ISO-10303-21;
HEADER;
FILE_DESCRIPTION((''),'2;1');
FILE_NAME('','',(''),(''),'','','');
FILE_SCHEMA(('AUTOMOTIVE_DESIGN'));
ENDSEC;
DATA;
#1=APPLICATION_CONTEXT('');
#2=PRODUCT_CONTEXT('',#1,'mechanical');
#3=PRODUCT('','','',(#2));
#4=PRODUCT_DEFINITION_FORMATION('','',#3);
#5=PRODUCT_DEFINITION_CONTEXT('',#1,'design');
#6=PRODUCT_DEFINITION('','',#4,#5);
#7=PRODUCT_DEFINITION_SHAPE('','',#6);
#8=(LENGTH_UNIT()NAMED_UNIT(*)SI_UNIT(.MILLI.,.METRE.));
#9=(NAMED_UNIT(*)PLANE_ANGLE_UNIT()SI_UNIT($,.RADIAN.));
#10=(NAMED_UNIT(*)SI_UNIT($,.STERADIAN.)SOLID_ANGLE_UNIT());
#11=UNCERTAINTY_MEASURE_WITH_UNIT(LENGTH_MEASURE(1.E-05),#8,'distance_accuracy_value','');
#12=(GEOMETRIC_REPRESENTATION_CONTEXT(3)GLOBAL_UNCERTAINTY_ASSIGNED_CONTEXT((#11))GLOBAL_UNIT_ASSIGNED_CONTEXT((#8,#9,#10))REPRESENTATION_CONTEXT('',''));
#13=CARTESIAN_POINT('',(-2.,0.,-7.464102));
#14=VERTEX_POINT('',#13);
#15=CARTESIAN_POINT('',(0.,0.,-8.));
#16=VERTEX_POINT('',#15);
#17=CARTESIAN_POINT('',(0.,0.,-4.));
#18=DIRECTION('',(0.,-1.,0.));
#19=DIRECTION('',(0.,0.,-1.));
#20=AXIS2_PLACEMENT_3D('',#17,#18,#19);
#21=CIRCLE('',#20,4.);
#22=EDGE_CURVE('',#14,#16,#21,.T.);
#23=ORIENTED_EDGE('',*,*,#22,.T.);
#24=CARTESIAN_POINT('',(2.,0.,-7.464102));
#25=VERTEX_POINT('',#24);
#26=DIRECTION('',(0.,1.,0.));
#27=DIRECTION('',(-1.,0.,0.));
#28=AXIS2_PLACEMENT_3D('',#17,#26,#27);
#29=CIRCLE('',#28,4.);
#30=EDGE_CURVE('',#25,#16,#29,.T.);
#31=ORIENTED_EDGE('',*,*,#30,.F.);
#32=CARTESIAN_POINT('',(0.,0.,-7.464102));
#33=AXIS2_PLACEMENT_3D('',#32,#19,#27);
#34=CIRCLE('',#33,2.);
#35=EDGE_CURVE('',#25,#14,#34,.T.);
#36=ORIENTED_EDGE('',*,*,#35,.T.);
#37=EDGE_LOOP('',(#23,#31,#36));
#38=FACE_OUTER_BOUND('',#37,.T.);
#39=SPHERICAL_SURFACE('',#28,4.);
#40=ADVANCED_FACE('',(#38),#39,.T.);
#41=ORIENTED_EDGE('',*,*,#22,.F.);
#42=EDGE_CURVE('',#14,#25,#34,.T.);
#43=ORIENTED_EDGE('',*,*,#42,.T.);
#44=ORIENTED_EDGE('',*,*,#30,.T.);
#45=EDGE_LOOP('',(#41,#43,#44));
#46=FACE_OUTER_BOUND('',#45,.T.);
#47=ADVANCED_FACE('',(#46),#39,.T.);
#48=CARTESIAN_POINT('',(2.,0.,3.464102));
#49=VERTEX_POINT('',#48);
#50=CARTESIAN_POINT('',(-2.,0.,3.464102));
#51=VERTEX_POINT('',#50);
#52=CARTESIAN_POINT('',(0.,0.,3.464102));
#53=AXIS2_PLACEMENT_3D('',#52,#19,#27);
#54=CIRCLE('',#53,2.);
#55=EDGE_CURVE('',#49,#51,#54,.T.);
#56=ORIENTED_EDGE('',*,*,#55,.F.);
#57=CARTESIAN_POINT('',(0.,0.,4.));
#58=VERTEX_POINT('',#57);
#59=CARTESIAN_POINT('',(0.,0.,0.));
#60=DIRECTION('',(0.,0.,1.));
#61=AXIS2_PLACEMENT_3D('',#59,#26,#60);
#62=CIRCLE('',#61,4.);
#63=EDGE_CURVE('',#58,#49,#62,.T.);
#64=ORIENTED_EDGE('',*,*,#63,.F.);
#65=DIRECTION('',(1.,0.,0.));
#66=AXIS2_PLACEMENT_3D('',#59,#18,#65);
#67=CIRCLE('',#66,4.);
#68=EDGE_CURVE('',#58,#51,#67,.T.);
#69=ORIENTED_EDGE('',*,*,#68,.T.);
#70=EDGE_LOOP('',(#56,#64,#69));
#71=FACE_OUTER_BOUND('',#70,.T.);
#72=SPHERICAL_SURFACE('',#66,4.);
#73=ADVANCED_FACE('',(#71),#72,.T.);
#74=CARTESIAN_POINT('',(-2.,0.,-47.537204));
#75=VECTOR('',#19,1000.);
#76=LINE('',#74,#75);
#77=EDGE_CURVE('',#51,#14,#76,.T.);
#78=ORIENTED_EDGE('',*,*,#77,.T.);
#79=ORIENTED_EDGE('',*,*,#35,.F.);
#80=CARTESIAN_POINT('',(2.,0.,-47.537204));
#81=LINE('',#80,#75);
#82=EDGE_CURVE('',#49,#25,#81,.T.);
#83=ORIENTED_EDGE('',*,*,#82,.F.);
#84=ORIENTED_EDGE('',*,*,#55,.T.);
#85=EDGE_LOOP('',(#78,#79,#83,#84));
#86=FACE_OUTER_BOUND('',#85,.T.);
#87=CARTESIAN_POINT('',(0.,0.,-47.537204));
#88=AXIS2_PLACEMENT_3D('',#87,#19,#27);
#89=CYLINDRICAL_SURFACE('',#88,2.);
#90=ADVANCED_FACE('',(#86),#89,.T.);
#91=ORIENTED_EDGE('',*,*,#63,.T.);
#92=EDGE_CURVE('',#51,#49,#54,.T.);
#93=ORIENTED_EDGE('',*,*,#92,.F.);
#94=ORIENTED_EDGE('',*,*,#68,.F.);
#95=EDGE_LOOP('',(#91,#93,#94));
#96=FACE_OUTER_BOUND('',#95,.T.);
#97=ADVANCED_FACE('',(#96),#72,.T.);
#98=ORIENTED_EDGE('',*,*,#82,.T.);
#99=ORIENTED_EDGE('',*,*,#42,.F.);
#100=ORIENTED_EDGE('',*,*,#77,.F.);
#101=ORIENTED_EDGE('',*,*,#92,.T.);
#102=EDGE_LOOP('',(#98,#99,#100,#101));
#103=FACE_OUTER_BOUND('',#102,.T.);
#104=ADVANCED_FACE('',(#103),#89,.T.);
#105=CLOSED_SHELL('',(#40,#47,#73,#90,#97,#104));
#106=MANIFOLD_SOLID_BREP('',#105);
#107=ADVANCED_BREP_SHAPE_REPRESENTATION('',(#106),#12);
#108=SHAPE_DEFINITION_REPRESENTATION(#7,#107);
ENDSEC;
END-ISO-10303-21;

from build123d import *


with BuildPart() as part:
    # Logo3_bib1 → Revolve1 (revolve)
    with BuildSketch(Plane(origin=(0, 0, 0), x_dir=(-1, 0, 0), z_dir=(0, -1, 0))):
        with BuildLine():
            Line((0, 8), (0, -4))
            ThreePointArc((0, -4), (1.03527618, -3.863703305), (2, -3.464101615))
            Line((2, -3.464101615), (2, 7.464101615))
            ThreePointArc((2, 7.464101615), (1.03527618, 7.863703305), (0, 8))
        make_face()
    revolve(axis=Axis((0, 0, -47.537203702), (0, 0, 1)))


solid = part.part
